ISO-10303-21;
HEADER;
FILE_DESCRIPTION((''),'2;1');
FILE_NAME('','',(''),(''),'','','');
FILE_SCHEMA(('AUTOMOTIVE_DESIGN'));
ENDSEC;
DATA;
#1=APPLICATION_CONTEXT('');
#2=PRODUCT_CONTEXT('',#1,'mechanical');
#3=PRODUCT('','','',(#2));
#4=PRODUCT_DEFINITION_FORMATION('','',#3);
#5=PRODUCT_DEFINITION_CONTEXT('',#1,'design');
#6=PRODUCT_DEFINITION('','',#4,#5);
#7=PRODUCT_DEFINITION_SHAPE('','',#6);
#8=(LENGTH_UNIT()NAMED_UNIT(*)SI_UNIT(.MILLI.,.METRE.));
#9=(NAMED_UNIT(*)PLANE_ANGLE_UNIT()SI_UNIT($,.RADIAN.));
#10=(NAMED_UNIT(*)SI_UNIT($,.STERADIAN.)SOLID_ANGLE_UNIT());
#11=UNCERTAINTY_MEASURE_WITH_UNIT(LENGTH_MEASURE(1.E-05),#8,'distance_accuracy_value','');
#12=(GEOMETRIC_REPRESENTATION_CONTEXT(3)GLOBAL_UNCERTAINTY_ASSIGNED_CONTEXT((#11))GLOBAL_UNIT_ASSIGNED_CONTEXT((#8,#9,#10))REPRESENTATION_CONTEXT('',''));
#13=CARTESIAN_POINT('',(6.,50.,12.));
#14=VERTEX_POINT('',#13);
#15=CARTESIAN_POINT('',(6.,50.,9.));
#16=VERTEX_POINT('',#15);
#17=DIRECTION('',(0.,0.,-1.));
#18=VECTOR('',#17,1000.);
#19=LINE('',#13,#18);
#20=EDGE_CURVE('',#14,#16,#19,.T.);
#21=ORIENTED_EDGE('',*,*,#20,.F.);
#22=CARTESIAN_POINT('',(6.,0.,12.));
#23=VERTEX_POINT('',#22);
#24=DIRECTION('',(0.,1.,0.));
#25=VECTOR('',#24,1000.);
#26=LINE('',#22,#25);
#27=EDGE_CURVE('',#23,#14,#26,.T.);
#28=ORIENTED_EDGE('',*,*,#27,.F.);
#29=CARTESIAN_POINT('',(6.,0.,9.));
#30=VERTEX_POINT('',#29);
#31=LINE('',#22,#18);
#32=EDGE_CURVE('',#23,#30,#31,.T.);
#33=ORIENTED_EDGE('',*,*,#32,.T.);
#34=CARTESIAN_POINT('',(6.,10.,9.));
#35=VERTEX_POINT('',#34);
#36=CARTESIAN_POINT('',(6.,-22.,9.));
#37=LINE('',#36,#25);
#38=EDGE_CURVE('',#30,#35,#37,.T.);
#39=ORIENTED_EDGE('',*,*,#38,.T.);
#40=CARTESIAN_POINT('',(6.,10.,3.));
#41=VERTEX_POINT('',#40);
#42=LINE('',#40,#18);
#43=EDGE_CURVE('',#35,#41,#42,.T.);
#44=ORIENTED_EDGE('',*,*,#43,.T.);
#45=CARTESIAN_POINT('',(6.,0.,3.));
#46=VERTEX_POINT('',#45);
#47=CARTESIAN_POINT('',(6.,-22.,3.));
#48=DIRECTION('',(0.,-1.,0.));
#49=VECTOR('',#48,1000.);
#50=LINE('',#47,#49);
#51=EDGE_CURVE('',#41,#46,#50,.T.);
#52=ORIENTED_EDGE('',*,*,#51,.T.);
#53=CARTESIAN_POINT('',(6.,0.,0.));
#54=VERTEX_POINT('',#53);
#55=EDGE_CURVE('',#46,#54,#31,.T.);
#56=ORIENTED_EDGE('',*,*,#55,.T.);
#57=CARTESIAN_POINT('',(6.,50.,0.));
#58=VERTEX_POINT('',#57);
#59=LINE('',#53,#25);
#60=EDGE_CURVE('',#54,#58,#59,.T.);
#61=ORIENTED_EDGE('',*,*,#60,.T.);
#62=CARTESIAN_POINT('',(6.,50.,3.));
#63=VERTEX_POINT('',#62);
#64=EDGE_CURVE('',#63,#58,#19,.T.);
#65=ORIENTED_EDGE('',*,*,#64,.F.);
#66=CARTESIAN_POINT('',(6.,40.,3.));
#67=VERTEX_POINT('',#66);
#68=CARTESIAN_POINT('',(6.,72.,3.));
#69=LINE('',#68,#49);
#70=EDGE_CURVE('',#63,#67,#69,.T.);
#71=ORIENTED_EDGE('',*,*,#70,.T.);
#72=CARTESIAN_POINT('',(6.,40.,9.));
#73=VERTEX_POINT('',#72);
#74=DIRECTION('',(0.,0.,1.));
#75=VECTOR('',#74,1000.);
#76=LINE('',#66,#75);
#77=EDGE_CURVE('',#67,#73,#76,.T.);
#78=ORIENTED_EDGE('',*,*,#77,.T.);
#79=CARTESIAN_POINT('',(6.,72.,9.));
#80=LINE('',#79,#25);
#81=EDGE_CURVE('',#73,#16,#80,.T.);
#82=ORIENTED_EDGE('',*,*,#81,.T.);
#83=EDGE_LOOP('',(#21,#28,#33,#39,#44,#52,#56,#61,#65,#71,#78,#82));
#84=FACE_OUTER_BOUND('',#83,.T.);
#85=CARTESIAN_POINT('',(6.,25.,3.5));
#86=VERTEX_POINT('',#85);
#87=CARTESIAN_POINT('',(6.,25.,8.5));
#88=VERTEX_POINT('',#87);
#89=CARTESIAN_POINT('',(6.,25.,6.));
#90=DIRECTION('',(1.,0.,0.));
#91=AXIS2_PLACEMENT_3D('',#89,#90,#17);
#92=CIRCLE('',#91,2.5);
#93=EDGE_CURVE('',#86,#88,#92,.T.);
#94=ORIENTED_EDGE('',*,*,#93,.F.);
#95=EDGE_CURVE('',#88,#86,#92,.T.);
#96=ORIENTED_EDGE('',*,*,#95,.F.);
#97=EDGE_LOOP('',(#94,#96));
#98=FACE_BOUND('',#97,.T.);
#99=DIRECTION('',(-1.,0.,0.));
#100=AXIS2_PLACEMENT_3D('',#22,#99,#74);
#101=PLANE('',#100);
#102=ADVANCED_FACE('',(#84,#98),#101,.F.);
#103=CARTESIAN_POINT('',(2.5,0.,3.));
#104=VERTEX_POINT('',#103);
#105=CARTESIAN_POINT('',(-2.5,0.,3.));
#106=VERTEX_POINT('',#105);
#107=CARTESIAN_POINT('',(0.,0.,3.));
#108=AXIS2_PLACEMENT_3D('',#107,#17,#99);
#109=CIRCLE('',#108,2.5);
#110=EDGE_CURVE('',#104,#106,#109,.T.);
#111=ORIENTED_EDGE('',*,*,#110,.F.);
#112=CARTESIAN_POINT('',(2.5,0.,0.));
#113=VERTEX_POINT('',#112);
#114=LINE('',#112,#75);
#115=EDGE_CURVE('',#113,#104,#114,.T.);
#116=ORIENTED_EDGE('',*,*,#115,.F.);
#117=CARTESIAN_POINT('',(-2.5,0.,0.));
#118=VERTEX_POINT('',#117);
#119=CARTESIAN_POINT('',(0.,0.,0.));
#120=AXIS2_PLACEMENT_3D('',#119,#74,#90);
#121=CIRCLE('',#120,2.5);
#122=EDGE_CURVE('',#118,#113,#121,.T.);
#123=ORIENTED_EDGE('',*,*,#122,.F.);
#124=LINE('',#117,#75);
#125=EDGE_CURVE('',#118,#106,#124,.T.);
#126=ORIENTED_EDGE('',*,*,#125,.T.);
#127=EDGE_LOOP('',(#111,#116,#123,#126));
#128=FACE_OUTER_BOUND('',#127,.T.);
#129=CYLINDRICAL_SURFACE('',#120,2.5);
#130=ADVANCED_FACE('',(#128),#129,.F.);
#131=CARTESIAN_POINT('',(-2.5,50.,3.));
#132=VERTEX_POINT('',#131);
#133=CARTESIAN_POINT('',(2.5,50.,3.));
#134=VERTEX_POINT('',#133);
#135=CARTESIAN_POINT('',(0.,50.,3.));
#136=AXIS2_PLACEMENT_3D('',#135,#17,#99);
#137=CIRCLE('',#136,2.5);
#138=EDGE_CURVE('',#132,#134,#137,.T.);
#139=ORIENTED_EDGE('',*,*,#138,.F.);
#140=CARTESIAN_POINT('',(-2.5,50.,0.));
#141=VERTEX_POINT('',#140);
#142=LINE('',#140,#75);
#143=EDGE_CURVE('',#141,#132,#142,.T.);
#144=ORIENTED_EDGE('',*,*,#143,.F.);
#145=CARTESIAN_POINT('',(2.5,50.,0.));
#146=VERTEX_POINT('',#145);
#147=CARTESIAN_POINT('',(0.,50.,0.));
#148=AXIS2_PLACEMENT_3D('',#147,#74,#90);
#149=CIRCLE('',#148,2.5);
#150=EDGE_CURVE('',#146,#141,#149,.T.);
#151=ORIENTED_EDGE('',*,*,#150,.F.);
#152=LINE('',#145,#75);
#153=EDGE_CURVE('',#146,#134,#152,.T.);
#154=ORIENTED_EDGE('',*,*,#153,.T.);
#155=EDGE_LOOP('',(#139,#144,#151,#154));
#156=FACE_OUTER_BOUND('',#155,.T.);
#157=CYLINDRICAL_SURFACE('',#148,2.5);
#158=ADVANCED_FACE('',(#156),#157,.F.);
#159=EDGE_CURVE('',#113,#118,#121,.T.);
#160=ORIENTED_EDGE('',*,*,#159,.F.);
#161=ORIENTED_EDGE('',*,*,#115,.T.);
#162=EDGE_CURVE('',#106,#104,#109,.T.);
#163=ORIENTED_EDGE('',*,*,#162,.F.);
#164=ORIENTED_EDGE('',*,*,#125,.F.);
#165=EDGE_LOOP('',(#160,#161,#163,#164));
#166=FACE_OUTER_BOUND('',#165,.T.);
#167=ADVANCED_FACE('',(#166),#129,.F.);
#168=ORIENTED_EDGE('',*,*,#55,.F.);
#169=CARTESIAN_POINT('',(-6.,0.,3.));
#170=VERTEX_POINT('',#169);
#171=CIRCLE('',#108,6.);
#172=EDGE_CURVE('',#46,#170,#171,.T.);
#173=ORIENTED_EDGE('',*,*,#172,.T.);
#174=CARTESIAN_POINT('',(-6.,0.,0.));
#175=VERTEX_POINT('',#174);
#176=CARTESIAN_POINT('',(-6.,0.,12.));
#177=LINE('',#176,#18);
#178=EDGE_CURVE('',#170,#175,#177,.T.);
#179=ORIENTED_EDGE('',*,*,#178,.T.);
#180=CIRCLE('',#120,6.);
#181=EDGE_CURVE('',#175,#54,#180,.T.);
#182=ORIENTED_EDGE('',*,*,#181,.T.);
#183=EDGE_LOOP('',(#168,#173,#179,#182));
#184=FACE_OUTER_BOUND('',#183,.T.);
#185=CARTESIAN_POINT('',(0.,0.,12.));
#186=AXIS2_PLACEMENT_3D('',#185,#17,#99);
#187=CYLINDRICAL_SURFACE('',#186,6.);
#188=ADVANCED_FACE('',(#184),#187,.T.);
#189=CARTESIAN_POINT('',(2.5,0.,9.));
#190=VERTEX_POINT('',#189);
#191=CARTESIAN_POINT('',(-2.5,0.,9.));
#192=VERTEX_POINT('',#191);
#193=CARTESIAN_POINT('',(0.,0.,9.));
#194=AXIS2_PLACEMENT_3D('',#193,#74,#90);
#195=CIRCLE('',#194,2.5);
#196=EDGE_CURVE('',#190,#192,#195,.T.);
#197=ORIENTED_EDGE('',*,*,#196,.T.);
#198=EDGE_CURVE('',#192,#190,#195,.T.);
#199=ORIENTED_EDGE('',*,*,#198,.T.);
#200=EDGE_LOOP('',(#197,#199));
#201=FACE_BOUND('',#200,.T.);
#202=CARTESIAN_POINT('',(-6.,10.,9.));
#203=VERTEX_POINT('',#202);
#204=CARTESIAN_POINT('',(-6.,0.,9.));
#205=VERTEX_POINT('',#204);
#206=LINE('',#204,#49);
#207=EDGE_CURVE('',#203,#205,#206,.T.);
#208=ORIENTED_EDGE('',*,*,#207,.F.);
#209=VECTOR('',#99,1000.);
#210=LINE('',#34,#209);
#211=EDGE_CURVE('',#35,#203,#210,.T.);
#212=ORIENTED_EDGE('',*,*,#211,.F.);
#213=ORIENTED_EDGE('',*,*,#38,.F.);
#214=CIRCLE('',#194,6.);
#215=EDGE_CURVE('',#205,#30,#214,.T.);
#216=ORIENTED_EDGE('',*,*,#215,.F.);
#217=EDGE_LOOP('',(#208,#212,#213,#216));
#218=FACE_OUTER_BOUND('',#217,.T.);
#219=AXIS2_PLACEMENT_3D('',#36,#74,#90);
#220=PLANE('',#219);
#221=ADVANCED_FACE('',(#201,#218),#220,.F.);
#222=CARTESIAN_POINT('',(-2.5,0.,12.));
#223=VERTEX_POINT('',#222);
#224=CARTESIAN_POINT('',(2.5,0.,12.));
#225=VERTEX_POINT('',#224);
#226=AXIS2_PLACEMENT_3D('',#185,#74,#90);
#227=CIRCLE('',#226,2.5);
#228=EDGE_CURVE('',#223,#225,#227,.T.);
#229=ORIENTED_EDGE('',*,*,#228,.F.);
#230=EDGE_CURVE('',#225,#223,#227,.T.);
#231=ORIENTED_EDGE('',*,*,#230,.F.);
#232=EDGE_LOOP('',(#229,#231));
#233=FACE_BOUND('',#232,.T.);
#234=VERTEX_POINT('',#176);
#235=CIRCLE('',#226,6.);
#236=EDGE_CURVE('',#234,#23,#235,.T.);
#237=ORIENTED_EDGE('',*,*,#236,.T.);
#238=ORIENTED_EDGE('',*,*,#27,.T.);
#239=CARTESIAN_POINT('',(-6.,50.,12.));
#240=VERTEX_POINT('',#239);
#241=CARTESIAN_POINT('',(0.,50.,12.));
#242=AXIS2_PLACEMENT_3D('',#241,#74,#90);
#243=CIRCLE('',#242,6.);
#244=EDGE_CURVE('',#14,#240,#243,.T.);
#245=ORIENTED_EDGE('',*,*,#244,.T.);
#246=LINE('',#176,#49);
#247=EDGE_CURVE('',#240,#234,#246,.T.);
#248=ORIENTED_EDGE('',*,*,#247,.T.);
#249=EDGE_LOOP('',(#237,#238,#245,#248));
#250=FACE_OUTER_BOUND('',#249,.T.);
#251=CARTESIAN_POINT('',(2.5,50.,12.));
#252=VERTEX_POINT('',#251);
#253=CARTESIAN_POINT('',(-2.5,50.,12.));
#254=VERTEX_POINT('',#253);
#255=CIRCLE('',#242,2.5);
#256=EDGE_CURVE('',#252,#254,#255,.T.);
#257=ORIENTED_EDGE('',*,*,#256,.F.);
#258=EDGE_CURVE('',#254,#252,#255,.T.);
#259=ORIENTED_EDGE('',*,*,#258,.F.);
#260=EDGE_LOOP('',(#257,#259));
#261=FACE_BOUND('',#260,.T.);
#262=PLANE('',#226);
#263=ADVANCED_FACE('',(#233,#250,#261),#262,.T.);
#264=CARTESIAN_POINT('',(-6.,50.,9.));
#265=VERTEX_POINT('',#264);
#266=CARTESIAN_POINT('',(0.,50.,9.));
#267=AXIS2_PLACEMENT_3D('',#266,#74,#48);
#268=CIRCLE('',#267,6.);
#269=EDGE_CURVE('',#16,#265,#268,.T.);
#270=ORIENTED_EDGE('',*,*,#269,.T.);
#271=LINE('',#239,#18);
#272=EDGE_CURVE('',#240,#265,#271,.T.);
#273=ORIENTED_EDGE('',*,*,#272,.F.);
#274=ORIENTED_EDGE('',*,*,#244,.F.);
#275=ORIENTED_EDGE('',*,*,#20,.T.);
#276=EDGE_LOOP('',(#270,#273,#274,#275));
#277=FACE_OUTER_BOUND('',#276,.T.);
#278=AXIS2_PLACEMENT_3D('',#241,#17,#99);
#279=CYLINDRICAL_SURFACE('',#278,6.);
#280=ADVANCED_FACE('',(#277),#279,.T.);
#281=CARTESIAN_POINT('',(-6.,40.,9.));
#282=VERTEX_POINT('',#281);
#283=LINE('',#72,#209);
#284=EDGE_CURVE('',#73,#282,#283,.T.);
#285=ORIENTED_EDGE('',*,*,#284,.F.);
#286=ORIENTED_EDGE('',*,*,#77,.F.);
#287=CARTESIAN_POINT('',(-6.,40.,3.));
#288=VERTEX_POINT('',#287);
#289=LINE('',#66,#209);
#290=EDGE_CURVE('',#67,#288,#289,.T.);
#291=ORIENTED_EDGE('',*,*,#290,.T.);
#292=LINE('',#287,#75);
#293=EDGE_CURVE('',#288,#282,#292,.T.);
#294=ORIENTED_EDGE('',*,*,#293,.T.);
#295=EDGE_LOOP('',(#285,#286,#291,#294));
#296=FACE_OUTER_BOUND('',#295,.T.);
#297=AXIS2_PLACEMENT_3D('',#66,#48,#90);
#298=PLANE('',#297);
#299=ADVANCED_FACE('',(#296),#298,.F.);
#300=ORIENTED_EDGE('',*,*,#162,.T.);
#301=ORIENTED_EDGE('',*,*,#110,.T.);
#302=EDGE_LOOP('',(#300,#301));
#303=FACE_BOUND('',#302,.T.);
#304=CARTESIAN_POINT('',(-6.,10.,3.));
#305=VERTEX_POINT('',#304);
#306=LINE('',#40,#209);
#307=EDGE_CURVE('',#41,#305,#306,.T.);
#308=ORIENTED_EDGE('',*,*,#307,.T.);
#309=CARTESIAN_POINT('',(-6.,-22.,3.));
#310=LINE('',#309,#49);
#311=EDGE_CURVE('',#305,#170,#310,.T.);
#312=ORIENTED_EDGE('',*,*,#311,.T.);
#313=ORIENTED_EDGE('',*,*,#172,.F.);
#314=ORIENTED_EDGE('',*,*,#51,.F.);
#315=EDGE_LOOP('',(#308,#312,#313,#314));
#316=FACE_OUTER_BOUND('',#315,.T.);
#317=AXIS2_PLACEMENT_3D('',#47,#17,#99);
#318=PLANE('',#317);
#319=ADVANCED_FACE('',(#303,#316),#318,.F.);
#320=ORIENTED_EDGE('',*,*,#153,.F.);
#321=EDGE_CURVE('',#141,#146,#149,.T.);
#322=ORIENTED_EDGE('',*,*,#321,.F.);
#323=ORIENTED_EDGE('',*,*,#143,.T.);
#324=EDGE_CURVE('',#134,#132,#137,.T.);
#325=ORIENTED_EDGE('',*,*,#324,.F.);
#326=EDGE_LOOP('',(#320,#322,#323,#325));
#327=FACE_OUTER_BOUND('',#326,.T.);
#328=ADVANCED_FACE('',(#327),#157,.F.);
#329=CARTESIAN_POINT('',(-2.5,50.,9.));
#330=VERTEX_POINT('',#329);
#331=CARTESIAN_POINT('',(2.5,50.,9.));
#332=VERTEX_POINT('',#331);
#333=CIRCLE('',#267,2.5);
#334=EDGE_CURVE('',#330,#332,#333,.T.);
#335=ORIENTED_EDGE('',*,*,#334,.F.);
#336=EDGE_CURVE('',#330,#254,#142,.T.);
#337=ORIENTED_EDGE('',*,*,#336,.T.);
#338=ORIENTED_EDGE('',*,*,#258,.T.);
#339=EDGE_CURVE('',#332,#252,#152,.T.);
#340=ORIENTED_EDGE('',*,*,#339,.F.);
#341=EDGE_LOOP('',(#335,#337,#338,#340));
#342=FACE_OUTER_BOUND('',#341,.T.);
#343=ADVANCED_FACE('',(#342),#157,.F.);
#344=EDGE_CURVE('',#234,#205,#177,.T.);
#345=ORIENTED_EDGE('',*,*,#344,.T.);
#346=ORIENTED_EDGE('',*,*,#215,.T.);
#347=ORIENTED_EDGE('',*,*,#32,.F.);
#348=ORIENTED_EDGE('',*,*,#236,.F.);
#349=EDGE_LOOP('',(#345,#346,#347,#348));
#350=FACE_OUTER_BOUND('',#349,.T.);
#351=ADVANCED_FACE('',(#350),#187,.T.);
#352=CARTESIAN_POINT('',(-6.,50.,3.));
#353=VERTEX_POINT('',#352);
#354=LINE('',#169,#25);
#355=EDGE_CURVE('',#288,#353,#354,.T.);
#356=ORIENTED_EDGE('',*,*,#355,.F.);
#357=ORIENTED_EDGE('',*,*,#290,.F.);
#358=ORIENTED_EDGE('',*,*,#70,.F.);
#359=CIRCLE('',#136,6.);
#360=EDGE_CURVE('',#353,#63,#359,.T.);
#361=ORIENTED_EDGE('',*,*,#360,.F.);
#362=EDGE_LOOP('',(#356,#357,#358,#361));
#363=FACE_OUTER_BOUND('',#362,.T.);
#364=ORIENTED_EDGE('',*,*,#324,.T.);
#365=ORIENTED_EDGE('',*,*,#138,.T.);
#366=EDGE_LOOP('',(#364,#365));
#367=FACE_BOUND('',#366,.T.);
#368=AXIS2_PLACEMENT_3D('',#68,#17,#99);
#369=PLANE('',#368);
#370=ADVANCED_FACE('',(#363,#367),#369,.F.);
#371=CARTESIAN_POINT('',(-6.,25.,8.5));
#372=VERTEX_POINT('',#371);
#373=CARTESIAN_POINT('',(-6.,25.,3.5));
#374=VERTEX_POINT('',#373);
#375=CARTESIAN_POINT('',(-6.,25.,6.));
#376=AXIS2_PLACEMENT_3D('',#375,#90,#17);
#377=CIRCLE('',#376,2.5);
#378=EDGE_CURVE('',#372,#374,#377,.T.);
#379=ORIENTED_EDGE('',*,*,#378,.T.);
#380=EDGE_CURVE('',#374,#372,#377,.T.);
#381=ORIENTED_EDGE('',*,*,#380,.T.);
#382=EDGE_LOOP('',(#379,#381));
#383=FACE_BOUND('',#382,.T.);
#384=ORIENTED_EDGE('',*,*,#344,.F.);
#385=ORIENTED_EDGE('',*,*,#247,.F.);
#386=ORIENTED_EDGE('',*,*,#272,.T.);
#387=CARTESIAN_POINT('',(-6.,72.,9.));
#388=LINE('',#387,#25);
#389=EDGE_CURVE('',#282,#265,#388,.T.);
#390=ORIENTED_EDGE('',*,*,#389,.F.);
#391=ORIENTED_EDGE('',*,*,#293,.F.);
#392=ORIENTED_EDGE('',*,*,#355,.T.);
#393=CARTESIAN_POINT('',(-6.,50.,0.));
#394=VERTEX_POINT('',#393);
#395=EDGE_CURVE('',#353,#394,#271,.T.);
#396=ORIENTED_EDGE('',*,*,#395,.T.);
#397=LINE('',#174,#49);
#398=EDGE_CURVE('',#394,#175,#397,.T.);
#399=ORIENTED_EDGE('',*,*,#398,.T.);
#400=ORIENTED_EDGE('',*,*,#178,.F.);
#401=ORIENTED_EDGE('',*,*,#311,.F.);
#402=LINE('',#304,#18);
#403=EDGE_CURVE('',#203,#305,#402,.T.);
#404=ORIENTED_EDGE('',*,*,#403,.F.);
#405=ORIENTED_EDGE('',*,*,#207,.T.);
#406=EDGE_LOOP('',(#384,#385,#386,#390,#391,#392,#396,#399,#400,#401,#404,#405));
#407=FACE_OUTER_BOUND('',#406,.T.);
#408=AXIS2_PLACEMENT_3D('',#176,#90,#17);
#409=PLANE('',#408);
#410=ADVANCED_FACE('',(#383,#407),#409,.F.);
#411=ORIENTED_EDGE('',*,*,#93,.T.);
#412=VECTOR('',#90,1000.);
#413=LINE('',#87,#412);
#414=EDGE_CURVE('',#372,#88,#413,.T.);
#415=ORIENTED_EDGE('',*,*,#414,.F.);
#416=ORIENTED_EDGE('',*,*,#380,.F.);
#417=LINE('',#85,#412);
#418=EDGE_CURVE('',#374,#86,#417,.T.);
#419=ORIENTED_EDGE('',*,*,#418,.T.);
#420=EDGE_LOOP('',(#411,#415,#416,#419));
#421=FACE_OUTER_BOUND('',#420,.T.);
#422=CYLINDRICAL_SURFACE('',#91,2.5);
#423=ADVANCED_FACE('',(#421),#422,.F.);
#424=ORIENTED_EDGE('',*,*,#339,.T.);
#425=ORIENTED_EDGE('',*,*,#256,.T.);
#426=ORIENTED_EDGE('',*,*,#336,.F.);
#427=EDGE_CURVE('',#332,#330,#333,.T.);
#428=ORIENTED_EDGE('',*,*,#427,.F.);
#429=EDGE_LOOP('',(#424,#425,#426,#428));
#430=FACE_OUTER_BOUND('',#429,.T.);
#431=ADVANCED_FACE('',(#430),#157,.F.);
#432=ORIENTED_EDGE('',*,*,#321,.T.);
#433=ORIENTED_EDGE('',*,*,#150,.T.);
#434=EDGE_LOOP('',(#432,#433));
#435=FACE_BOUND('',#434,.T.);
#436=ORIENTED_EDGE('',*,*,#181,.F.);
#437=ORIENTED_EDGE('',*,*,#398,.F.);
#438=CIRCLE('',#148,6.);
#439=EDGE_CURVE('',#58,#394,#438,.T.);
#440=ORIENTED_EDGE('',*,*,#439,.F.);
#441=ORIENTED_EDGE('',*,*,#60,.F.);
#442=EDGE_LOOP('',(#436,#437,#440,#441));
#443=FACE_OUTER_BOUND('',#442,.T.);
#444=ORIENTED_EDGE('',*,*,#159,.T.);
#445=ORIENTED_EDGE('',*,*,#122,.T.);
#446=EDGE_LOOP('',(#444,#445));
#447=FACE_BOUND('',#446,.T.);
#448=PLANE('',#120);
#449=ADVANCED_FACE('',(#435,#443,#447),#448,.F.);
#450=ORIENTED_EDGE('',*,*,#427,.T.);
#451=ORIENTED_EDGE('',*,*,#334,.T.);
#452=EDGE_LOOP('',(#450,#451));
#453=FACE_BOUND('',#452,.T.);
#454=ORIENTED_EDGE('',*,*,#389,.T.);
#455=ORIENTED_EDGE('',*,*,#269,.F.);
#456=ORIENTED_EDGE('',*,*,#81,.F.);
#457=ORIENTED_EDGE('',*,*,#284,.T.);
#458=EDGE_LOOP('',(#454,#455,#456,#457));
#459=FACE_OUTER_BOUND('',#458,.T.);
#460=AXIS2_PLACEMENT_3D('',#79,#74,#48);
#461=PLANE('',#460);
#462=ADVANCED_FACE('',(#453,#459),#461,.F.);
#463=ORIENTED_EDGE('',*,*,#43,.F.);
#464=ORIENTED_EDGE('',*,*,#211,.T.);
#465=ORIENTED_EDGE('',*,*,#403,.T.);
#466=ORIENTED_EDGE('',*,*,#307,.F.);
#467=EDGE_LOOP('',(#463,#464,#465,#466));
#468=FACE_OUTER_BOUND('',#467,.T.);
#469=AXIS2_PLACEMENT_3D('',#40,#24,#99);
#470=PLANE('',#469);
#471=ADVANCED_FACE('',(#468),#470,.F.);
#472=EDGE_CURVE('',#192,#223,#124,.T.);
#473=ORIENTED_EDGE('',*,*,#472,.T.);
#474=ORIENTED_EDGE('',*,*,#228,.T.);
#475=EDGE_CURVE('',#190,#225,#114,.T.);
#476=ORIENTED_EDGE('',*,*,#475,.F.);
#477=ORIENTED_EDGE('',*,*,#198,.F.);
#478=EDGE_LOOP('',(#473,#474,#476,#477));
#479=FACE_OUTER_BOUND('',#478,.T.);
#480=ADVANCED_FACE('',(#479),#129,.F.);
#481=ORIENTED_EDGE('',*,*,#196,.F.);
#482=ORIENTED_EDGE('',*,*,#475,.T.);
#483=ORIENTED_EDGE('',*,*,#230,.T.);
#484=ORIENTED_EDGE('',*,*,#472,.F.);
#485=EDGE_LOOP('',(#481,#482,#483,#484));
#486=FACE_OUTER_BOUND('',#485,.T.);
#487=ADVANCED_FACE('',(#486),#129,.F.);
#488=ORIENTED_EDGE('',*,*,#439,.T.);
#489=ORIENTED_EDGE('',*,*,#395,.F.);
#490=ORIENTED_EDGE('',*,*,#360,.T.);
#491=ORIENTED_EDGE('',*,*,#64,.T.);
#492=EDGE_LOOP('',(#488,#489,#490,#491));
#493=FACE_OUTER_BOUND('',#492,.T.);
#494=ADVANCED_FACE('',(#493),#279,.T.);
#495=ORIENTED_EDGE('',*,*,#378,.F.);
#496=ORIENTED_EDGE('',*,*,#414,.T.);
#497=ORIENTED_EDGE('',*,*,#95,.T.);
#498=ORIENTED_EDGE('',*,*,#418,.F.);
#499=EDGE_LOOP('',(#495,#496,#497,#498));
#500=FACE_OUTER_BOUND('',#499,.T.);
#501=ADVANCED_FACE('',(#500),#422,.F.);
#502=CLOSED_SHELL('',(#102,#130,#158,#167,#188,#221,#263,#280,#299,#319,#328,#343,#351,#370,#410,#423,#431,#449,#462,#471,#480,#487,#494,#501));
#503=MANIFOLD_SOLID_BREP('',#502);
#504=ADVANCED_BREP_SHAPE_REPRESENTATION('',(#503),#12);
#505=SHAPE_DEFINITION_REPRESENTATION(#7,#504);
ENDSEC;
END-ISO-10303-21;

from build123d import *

# Parameters (mm, degrees)
BOSS_EXTRUDE1_DEPTH = 12
SKETCH2_W           = 6
SKETCH2_H           = 32
CUT_EXTRUDE1_DEPTH  = 59.514955353
SKETCH3_R           = 2.5
CUT_EXTRUDE2_DEPTH  = 58.584720196
M6_TAPPED_HOLE1_D   = 5


with BuildPart() as part:
    # Sketch1 → Boss-Extrude1 (new body)
    with BuildSketch(Plane.XY):
        with BuildLine():
            Line((-6, 0), (-6, 50))
            ThreePointArc((-6, 50), (0, 56), (6, 50))
            Line((6, 50), (6, 0))
            ThreePointArc((6, 0), (0, -6), (-6, 0))
        make_face()
    extrude(amount=BOSS_EXTRUDE1_DEPTH)

    # Sketch2 → Cut-Extrude1 (cut, through all)
    with BuildSketch(Plane.ZY.offset(6)):
        with Locations((6, 56)):
            Rectangle(SKETCH2_W, SKETCH2_H)
        with Locations((6, -6)):
            Rectangle(SKETCH2_W, SKETCH2_H)
    extrude(amount=-CUT_EXTRUDE1_DEPTH, mode=Mode.SUBTRACT)

    # Sketch3 → Cut-Extrude2 (cut, through all)
    with BuildSketch(Plane.XY.offset(12)):
        with Locations((0, 50)):
            Circle(SKETCH3_R)
        Circle(SKETCH3_R)
    extrude(amount=-CUT_EXTRUDE2_DEPTH, mode=Mode.SUBTRACT)

    # M6 Tapped Hole1 (through all)
    with Locations(Plane(origin=(6, 25, 6), x_dir=(0, 0, 1), z_dir=(1, 0, 0))):
        with Locations((0, 0)):
            Hole(M6_TAPPED_HOLE1_D / 2)


solid = part.part
